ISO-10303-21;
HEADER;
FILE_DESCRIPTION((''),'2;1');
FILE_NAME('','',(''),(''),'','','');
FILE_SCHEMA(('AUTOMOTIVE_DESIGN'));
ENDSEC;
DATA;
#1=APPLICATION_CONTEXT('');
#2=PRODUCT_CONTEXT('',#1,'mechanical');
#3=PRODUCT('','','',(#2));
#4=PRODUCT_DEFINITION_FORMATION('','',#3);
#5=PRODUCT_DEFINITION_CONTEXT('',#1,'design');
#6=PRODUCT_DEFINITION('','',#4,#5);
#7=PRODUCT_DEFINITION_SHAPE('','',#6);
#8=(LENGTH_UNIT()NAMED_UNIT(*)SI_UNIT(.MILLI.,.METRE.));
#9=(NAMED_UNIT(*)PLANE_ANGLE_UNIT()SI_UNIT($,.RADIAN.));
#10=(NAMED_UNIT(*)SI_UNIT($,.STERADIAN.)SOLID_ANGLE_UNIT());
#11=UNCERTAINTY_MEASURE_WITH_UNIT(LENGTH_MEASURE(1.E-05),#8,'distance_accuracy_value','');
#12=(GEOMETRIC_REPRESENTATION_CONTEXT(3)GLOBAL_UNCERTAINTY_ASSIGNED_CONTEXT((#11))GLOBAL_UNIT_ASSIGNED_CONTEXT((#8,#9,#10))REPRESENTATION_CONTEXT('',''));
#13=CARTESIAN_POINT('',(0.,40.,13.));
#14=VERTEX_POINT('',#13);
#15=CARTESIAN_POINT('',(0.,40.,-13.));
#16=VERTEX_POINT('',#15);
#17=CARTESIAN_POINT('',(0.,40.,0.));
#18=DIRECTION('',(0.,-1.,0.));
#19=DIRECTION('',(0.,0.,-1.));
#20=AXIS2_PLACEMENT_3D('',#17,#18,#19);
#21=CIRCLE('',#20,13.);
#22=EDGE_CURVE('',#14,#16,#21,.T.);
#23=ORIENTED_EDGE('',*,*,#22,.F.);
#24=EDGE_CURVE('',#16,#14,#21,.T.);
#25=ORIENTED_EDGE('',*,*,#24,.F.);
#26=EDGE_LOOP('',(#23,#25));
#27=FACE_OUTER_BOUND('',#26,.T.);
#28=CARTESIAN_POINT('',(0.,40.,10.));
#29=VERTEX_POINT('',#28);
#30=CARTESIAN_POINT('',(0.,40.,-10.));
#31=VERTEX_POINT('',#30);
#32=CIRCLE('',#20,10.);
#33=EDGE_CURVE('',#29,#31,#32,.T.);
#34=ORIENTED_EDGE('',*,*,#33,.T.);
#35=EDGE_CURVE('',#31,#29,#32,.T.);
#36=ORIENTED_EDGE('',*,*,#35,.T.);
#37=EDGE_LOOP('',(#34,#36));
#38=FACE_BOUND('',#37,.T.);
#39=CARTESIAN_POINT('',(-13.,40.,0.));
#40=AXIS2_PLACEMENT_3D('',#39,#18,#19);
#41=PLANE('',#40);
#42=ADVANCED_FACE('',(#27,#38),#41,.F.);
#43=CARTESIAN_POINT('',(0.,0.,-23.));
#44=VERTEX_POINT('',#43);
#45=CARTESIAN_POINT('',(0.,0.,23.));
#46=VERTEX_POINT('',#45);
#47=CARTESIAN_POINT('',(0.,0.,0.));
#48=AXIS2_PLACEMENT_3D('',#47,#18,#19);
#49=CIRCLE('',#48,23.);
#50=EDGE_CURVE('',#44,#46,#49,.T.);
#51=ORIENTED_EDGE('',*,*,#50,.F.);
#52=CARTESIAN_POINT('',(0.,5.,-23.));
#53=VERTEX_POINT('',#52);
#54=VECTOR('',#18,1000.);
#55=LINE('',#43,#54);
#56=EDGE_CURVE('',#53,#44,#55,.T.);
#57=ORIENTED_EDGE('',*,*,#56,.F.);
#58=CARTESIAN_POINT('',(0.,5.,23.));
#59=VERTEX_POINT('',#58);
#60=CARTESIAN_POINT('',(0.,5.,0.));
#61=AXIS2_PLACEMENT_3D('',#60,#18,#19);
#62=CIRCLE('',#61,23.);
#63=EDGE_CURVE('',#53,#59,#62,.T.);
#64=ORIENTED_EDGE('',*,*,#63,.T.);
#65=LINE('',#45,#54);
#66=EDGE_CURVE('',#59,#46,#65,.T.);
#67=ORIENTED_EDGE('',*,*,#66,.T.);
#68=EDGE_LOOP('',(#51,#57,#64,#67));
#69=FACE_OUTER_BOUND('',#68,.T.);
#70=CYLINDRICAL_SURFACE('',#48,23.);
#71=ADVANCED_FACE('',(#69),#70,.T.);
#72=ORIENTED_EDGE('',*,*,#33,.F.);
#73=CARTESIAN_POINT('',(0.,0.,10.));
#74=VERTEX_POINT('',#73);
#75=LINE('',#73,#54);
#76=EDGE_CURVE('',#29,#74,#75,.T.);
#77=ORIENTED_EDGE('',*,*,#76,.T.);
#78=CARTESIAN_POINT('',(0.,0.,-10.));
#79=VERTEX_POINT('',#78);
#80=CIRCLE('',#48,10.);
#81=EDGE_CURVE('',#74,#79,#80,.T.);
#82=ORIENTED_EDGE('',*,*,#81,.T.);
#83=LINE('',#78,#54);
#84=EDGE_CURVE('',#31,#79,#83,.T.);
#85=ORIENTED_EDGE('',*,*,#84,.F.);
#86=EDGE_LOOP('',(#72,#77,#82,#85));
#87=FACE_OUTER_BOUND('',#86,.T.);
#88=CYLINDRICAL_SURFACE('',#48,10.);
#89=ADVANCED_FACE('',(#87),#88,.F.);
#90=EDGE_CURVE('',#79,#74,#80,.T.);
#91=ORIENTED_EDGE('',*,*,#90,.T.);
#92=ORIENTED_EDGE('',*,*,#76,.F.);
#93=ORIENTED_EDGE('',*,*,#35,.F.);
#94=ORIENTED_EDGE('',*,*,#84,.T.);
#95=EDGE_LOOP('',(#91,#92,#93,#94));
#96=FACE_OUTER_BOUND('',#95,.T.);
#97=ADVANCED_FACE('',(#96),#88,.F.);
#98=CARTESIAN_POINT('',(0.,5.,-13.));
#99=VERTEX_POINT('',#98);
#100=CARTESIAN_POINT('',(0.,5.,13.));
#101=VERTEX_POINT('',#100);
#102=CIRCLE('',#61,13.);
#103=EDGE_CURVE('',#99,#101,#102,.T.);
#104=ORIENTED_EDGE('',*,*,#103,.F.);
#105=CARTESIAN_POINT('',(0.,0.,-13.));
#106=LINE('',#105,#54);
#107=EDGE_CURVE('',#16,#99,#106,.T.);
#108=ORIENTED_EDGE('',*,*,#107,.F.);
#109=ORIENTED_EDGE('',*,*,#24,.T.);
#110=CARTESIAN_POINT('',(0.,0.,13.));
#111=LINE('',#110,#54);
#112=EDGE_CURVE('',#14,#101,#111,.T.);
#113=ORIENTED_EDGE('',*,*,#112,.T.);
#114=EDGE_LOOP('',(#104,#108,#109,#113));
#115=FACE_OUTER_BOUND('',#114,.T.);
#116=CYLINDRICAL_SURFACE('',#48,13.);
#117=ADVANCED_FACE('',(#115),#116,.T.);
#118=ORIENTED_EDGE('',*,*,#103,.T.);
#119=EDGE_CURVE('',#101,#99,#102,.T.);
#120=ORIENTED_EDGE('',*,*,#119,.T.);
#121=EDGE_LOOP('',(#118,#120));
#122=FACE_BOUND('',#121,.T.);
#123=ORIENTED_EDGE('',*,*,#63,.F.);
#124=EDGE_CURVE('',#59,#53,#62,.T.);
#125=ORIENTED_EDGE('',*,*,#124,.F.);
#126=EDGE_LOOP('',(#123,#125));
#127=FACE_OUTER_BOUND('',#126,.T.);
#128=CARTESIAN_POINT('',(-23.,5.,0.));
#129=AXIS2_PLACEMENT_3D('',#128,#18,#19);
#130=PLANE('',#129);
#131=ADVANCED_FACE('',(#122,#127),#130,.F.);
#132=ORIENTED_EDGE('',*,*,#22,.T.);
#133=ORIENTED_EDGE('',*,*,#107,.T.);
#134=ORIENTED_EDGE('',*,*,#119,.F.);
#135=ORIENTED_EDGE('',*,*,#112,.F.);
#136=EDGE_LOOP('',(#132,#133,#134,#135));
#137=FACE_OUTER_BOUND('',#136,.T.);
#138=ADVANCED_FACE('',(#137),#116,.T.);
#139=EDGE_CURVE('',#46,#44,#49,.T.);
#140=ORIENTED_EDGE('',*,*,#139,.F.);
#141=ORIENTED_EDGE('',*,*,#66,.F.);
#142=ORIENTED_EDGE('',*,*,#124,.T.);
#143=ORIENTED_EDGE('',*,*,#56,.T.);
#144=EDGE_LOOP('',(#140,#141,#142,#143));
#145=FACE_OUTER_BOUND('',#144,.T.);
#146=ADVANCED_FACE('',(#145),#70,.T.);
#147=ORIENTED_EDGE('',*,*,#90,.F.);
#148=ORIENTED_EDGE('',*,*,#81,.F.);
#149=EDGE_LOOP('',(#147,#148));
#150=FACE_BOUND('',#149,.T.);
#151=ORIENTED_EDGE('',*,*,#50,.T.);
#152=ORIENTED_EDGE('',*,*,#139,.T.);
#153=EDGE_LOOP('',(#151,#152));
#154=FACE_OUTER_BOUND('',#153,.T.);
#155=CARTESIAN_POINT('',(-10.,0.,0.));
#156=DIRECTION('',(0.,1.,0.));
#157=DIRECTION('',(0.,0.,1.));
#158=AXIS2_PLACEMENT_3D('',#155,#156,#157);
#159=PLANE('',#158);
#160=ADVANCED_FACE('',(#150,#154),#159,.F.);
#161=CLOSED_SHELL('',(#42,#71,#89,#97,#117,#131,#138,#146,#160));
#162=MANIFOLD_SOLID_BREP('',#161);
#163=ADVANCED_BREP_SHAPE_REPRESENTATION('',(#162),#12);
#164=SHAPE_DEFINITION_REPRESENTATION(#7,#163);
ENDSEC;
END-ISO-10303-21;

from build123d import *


with BuildPart() as part:
    # 草图1 → 旋转1 (revolve)
    with BuildSketch(Plane.XY, mode=Mode.PRIVATE) as revolve_1_sk:
        Polygon((-10, 0), (-23, 0), (-23, 5), (-13, 5), (-13, 40), (-10, 40), align=None)
    revolve(revolve_1_sk.sketch.rotate(Axis((0, 0, 0), (0, 1, 0)), 270), axis=Axis((0, 0, 0), (0, 1, 0)))


solid = part.part
